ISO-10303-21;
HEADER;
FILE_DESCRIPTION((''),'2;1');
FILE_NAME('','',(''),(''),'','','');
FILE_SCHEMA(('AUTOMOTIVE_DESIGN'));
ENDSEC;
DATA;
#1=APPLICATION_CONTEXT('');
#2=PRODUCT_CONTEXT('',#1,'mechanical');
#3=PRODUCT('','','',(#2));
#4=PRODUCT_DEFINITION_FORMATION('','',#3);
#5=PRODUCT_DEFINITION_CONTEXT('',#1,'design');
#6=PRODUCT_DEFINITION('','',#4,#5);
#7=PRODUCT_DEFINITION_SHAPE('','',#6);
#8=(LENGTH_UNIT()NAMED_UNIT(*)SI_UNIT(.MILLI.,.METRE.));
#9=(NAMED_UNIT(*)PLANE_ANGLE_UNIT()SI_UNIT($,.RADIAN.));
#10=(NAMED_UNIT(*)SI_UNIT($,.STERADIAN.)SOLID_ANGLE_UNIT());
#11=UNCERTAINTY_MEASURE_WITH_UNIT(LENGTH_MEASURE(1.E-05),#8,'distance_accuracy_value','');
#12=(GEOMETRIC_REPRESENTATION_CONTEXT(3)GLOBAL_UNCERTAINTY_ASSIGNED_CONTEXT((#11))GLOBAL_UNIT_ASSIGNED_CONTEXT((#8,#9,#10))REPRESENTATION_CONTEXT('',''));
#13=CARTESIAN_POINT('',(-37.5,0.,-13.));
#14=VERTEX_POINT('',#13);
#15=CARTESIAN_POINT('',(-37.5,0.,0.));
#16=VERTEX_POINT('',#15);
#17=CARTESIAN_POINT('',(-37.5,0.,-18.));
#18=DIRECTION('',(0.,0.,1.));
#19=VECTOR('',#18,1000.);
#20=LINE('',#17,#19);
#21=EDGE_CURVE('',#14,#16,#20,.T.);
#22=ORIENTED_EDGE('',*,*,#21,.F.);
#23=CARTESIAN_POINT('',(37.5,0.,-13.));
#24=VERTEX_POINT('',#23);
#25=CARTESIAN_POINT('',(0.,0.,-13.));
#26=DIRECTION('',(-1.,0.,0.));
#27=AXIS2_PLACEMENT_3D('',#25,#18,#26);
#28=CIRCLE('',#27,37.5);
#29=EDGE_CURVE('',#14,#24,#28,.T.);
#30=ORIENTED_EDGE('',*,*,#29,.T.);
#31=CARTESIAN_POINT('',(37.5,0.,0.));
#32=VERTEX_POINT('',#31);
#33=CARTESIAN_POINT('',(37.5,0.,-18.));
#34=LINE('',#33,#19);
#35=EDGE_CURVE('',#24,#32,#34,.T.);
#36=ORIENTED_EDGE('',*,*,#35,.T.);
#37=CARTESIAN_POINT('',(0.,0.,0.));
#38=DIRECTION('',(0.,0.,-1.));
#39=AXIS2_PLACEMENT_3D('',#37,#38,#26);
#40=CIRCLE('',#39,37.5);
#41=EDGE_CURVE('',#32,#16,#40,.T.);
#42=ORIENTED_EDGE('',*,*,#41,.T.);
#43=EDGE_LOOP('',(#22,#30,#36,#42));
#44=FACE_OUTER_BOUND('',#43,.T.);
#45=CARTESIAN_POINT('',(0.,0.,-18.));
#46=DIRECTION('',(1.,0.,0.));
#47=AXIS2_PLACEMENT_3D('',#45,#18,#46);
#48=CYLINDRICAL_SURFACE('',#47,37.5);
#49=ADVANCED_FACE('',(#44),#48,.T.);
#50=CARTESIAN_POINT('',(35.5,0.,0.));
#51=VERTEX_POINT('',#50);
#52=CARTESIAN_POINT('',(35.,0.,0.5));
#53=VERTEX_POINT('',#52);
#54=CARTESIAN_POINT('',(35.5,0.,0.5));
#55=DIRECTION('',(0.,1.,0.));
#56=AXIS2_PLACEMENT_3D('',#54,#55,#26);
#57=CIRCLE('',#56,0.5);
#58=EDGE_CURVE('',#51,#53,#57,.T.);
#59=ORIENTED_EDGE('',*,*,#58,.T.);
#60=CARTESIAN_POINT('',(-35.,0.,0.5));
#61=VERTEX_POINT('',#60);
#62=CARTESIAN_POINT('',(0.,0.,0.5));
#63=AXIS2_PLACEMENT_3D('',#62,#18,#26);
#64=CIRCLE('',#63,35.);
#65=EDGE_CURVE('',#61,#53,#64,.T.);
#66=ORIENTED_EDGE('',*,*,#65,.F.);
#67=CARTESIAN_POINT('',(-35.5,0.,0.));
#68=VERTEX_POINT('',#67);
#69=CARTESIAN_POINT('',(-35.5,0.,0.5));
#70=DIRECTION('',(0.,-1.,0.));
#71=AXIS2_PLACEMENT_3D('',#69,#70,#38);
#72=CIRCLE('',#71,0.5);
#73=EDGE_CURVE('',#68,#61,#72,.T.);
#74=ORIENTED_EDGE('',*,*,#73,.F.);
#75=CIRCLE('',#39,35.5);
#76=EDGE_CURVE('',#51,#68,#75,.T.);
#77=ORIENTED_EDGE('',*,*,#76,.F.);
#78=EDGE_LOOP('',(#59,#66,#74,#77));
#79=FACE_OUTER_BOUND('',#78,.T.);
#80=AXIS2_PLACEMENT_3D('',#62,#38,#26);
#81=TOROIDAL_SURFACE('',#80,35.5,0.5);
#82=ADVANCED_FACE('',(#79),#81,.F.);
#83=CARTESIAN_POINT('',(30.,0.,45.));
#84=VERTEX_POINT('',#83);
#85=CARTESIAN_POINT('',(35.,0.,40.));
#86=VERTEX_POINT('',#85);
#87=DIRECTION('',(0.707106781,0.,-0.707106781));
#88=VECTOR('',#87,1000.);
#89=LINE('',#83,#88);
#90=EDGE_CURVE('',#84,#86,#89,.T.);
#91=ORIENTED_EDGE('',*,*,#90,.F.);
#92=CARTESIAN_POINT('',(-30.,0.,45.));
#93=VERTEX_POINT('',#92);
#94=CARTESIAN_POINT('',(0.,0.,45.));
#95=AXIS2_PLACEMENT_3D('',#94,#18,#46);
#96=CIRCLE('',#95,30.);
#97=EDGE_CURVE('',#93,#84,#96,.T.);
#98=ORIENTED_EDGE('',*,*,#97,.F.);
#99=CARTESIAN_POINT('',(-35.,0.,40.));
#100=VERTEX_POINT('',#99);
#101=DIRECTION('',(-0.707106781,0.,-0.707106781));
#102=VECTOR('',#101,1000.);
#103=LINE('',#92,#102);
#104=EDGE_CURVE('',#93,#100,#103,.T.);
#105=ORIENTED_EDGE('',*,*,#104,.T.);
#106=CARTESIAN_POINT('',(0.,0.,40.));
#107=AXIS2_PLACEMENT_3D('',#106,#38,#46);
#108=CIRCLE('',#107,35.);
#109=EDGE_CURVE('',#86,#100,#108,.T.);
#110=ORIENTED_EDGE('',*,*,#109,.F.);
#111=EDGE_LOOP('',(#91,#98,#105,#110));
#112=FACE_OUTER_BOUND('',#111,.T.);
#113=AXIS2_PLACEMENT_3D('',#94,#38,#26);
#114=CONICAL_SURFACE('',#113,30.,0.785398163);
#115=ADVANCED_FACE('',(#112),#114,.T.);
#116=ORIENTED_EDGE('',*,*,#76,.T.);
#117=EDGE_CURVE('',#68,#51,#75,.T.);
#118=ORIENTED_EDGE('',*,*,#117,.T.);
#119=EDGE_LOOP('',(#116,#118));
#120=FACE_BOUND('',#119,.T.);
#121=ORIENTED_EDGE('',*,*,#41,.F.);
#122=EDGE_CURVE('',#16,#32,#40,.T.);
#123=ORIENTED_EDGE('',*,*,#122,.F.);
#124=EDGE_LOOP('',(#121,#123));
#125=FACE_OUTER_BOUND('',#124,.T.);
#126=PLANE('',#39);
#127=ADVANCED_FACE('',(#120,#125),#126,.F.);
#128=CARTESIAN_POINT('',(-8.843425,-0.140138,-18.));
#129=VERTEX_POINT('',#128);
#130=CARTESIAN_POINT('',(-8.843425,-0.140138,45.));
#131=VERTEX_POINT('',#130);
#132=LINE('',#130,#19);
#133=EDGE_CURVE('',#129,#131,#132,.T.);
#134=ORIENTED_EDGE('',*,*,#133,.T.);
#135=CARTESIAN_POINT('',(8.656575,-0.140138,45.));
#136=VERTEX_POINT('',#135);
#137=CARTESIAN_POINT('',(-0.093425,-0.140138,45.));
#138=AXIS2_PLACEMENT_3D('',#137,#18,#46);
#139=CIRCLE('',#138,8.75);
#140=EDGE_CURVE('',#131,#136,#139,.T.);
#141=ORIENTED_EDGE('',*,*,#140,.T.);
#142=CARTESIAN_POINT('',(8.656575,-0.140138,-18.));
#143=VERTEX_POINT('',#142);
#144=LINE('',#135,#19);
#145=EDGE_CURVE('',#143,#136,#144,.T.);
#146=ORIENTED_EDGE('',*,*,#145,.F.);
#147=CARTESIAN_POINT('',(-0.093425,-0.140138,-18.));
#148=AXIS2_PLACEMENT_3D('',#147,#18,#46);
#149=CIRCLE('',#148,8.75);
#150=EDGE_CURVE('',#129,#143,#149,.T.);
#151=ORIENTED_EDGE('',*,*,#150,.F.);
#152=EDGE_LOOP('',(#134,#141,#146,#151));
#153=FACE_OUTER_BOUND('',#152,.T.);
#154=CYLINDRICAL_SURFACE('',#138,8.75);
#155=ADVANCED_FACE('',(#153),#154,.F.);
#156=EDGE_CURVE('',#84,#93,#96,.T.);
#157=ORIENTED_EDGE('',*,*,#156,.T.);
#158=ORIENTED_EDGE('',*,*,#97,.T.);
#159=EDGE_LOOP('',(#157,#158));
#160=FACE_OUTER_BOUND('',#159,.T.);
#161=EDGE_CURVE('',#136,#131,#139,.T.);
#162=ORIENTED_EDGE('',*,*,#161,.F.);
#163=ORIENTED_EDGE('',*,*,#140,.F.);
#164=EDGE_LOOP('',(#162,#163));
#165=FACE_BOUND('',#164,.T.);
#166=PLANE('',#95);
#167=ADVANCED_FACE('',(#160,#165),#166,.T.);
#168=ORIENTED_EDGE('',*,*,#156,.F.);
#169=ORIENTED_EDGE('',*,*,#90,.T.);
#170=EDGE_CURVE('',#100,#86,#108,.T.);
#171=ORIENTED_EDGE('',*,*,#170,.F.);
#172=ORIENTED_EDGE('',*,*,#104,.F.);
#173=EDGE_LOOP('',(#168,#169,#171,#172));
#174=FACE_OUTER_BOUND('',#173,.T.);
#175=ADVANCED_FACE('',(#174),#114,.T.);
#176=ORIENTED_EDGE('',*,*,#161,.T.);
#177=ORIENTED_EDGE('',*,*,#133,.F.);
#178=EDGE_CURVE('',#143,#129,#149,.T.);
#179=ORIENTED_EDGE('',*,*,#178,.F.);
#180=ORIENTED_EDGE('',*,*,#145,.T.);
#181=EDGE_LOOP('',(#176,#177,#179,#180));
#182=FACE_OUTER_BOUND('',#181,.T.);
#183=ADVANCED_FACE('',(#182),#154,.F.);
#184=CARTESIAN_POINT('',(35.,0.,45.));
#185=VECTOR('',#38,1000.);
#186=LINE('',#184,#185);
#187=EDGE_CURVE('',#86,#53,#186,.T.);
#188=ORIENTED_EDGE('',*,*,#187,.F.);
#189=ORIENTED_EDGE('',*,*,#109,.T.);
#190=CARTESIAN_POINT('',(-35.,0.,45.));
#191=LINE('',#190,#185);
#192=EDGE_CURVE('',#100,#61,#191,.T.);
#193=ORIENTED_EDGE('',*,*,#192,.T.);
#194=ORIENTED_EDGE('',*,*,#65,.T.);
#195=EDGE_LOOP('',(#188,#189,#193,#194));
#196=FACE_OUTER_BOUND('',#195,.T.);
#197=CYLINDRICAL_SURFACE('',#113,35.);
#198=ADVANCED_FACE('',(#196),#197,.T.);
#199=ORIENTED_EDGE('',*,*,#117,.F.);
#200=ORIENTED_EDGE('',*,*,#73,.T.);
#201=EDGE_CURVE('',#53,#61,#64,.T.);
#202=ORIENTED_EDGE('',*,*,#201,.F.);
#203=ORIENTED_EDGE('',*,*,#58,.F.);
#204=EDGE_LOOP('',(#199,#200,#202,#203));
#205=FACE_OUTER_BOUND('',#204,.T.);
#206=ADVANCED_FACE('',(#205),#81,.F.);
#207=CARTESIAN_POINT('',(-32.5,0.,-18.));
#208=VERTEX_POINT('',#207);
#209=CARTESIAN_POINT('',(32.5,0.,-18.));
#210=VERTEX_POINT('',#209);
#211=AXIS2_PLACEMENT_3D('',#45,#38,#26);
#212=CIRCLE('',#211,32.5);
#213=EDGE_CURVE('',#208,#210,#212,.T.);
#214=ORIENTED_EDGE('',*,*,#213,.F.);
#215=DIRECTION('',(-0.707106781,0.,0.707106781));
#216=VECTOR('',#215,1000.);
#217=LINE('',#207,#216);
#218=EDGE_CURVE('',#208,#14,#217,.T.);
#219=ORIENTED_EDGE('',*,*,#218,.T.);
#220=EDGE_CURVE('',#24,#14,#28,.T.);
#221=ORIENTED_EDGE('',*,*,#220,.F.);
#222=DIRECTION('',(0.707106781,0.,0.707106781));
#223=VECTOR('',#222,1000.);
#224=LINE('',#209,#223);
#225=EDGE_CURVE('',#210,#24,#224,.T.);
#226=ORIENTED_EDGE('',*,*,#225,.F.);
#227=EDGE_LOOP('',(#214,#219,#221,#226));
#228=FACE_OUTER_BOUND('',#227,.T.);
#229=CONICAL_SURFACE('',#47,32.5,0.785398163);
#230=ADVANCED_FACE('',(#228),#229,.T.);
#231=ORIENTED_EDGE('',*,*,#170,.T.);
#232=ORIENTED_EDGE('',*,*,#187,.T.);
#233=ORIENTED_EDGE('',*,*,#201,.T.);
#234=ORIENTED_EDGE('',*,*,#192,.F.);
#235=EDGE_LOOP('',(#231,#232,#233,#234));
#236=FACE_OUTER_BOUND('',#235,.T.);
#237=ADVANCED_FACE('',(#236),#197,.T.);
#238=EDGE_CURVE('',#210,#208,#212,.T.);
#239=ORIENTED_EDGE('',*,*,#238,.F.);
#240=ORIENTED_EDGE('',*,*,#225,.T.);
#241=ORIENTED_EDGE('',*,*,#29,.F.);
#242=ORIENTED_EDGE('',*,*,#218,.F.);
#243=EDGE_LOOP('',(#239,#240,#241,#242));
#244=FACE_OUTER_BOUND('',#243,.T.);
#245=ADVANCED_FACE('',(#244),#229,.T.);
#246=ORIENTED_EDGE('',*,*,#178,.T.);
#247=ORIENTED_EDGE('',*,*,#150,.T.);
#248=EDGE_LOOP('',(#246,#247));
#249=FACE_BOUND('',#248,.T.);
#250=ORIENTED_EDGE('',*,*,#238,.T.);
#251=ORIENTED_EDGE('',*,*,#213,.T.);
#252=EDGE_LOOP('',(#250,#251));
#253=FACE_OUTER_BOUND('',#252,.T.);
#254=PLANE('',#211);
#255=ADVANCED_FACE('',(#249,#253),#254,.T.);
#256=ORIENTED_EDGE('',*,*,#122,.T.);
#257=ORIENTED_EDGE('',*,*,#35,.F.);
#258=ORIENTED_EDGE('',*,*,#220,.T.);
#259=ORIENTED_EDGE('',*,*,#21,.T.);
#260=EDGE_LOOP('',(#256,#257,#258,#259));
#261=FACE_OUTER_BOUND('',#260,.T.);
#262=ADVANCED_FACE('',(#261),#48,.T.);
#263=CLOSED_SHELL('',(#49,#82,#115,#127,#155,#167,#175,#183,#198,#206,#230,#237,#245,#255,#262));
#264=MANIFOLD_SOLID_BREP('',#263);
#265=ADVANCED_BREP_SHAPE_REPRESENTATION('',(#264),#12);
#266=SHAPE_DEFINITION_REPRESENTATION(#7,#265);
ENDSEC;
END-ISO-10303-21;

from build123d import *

# Parameters (mm, degrees)
SKETCH_1_R          = 35
EXTRUDE_1_DEPTH     = 45
SKETCH_5_R          = 37.5
EXTRUDE_2_DEPTH     = 18
CHAMFER_1_SIZE      = 5
HOLE_WIZARD_M20_1_D = 17.5
FILLET_1_R          = 0.5


with BuildPart() as part:
    # 草图1 → 凸台-拉伸1 (new body)
    with BuildSketch(Plane.XY):
        with Locations(Location((0, 0, 0), (0, 0, 180))):
            Circle(SKETCH_1_R)
    extrude(amount=EXTRUDE_1_DEPTH)

    # 草图5 → 凸台-拉伸2 (add)
    with BuildSketch(Plane(origin=(0, 0, 0), x_dir=(-1, 0, 0), z_dir=(0, 0, -1))):
        Circle(SKETCH_5_R)
    extrude(amount=EXTRUDE_2_DEPTH)

    # 倒角1
    chamfer_1_edges = [part.edges().sort_by_distance(p)[0] for p in [
        (35, 0, 45),
        (37.5, 0, -18),
    ]]
    chamfer(chamfer_1_edges, length=CHAMFER_1_SIZE)

    # M20 螺纹孔1 (through all)
    with Locations(Plane(origin=(-0.093425474, -0.140138211, 45), x_dir=(1, 0, 0), z_dir=(0, 0, 1))):
        with Locations((0, 0)):
            Hole(HOLE_WIZARD_M20_1_D / 2)

    # 圆角1
    fillet_1_edges = [part.edges().sort_by_distance(p)[0] for p in [
        (35, 0, 0),
    ]]
    fillet(fillet_1_edges, radius=FILLET_1_R)


solid = part.part
